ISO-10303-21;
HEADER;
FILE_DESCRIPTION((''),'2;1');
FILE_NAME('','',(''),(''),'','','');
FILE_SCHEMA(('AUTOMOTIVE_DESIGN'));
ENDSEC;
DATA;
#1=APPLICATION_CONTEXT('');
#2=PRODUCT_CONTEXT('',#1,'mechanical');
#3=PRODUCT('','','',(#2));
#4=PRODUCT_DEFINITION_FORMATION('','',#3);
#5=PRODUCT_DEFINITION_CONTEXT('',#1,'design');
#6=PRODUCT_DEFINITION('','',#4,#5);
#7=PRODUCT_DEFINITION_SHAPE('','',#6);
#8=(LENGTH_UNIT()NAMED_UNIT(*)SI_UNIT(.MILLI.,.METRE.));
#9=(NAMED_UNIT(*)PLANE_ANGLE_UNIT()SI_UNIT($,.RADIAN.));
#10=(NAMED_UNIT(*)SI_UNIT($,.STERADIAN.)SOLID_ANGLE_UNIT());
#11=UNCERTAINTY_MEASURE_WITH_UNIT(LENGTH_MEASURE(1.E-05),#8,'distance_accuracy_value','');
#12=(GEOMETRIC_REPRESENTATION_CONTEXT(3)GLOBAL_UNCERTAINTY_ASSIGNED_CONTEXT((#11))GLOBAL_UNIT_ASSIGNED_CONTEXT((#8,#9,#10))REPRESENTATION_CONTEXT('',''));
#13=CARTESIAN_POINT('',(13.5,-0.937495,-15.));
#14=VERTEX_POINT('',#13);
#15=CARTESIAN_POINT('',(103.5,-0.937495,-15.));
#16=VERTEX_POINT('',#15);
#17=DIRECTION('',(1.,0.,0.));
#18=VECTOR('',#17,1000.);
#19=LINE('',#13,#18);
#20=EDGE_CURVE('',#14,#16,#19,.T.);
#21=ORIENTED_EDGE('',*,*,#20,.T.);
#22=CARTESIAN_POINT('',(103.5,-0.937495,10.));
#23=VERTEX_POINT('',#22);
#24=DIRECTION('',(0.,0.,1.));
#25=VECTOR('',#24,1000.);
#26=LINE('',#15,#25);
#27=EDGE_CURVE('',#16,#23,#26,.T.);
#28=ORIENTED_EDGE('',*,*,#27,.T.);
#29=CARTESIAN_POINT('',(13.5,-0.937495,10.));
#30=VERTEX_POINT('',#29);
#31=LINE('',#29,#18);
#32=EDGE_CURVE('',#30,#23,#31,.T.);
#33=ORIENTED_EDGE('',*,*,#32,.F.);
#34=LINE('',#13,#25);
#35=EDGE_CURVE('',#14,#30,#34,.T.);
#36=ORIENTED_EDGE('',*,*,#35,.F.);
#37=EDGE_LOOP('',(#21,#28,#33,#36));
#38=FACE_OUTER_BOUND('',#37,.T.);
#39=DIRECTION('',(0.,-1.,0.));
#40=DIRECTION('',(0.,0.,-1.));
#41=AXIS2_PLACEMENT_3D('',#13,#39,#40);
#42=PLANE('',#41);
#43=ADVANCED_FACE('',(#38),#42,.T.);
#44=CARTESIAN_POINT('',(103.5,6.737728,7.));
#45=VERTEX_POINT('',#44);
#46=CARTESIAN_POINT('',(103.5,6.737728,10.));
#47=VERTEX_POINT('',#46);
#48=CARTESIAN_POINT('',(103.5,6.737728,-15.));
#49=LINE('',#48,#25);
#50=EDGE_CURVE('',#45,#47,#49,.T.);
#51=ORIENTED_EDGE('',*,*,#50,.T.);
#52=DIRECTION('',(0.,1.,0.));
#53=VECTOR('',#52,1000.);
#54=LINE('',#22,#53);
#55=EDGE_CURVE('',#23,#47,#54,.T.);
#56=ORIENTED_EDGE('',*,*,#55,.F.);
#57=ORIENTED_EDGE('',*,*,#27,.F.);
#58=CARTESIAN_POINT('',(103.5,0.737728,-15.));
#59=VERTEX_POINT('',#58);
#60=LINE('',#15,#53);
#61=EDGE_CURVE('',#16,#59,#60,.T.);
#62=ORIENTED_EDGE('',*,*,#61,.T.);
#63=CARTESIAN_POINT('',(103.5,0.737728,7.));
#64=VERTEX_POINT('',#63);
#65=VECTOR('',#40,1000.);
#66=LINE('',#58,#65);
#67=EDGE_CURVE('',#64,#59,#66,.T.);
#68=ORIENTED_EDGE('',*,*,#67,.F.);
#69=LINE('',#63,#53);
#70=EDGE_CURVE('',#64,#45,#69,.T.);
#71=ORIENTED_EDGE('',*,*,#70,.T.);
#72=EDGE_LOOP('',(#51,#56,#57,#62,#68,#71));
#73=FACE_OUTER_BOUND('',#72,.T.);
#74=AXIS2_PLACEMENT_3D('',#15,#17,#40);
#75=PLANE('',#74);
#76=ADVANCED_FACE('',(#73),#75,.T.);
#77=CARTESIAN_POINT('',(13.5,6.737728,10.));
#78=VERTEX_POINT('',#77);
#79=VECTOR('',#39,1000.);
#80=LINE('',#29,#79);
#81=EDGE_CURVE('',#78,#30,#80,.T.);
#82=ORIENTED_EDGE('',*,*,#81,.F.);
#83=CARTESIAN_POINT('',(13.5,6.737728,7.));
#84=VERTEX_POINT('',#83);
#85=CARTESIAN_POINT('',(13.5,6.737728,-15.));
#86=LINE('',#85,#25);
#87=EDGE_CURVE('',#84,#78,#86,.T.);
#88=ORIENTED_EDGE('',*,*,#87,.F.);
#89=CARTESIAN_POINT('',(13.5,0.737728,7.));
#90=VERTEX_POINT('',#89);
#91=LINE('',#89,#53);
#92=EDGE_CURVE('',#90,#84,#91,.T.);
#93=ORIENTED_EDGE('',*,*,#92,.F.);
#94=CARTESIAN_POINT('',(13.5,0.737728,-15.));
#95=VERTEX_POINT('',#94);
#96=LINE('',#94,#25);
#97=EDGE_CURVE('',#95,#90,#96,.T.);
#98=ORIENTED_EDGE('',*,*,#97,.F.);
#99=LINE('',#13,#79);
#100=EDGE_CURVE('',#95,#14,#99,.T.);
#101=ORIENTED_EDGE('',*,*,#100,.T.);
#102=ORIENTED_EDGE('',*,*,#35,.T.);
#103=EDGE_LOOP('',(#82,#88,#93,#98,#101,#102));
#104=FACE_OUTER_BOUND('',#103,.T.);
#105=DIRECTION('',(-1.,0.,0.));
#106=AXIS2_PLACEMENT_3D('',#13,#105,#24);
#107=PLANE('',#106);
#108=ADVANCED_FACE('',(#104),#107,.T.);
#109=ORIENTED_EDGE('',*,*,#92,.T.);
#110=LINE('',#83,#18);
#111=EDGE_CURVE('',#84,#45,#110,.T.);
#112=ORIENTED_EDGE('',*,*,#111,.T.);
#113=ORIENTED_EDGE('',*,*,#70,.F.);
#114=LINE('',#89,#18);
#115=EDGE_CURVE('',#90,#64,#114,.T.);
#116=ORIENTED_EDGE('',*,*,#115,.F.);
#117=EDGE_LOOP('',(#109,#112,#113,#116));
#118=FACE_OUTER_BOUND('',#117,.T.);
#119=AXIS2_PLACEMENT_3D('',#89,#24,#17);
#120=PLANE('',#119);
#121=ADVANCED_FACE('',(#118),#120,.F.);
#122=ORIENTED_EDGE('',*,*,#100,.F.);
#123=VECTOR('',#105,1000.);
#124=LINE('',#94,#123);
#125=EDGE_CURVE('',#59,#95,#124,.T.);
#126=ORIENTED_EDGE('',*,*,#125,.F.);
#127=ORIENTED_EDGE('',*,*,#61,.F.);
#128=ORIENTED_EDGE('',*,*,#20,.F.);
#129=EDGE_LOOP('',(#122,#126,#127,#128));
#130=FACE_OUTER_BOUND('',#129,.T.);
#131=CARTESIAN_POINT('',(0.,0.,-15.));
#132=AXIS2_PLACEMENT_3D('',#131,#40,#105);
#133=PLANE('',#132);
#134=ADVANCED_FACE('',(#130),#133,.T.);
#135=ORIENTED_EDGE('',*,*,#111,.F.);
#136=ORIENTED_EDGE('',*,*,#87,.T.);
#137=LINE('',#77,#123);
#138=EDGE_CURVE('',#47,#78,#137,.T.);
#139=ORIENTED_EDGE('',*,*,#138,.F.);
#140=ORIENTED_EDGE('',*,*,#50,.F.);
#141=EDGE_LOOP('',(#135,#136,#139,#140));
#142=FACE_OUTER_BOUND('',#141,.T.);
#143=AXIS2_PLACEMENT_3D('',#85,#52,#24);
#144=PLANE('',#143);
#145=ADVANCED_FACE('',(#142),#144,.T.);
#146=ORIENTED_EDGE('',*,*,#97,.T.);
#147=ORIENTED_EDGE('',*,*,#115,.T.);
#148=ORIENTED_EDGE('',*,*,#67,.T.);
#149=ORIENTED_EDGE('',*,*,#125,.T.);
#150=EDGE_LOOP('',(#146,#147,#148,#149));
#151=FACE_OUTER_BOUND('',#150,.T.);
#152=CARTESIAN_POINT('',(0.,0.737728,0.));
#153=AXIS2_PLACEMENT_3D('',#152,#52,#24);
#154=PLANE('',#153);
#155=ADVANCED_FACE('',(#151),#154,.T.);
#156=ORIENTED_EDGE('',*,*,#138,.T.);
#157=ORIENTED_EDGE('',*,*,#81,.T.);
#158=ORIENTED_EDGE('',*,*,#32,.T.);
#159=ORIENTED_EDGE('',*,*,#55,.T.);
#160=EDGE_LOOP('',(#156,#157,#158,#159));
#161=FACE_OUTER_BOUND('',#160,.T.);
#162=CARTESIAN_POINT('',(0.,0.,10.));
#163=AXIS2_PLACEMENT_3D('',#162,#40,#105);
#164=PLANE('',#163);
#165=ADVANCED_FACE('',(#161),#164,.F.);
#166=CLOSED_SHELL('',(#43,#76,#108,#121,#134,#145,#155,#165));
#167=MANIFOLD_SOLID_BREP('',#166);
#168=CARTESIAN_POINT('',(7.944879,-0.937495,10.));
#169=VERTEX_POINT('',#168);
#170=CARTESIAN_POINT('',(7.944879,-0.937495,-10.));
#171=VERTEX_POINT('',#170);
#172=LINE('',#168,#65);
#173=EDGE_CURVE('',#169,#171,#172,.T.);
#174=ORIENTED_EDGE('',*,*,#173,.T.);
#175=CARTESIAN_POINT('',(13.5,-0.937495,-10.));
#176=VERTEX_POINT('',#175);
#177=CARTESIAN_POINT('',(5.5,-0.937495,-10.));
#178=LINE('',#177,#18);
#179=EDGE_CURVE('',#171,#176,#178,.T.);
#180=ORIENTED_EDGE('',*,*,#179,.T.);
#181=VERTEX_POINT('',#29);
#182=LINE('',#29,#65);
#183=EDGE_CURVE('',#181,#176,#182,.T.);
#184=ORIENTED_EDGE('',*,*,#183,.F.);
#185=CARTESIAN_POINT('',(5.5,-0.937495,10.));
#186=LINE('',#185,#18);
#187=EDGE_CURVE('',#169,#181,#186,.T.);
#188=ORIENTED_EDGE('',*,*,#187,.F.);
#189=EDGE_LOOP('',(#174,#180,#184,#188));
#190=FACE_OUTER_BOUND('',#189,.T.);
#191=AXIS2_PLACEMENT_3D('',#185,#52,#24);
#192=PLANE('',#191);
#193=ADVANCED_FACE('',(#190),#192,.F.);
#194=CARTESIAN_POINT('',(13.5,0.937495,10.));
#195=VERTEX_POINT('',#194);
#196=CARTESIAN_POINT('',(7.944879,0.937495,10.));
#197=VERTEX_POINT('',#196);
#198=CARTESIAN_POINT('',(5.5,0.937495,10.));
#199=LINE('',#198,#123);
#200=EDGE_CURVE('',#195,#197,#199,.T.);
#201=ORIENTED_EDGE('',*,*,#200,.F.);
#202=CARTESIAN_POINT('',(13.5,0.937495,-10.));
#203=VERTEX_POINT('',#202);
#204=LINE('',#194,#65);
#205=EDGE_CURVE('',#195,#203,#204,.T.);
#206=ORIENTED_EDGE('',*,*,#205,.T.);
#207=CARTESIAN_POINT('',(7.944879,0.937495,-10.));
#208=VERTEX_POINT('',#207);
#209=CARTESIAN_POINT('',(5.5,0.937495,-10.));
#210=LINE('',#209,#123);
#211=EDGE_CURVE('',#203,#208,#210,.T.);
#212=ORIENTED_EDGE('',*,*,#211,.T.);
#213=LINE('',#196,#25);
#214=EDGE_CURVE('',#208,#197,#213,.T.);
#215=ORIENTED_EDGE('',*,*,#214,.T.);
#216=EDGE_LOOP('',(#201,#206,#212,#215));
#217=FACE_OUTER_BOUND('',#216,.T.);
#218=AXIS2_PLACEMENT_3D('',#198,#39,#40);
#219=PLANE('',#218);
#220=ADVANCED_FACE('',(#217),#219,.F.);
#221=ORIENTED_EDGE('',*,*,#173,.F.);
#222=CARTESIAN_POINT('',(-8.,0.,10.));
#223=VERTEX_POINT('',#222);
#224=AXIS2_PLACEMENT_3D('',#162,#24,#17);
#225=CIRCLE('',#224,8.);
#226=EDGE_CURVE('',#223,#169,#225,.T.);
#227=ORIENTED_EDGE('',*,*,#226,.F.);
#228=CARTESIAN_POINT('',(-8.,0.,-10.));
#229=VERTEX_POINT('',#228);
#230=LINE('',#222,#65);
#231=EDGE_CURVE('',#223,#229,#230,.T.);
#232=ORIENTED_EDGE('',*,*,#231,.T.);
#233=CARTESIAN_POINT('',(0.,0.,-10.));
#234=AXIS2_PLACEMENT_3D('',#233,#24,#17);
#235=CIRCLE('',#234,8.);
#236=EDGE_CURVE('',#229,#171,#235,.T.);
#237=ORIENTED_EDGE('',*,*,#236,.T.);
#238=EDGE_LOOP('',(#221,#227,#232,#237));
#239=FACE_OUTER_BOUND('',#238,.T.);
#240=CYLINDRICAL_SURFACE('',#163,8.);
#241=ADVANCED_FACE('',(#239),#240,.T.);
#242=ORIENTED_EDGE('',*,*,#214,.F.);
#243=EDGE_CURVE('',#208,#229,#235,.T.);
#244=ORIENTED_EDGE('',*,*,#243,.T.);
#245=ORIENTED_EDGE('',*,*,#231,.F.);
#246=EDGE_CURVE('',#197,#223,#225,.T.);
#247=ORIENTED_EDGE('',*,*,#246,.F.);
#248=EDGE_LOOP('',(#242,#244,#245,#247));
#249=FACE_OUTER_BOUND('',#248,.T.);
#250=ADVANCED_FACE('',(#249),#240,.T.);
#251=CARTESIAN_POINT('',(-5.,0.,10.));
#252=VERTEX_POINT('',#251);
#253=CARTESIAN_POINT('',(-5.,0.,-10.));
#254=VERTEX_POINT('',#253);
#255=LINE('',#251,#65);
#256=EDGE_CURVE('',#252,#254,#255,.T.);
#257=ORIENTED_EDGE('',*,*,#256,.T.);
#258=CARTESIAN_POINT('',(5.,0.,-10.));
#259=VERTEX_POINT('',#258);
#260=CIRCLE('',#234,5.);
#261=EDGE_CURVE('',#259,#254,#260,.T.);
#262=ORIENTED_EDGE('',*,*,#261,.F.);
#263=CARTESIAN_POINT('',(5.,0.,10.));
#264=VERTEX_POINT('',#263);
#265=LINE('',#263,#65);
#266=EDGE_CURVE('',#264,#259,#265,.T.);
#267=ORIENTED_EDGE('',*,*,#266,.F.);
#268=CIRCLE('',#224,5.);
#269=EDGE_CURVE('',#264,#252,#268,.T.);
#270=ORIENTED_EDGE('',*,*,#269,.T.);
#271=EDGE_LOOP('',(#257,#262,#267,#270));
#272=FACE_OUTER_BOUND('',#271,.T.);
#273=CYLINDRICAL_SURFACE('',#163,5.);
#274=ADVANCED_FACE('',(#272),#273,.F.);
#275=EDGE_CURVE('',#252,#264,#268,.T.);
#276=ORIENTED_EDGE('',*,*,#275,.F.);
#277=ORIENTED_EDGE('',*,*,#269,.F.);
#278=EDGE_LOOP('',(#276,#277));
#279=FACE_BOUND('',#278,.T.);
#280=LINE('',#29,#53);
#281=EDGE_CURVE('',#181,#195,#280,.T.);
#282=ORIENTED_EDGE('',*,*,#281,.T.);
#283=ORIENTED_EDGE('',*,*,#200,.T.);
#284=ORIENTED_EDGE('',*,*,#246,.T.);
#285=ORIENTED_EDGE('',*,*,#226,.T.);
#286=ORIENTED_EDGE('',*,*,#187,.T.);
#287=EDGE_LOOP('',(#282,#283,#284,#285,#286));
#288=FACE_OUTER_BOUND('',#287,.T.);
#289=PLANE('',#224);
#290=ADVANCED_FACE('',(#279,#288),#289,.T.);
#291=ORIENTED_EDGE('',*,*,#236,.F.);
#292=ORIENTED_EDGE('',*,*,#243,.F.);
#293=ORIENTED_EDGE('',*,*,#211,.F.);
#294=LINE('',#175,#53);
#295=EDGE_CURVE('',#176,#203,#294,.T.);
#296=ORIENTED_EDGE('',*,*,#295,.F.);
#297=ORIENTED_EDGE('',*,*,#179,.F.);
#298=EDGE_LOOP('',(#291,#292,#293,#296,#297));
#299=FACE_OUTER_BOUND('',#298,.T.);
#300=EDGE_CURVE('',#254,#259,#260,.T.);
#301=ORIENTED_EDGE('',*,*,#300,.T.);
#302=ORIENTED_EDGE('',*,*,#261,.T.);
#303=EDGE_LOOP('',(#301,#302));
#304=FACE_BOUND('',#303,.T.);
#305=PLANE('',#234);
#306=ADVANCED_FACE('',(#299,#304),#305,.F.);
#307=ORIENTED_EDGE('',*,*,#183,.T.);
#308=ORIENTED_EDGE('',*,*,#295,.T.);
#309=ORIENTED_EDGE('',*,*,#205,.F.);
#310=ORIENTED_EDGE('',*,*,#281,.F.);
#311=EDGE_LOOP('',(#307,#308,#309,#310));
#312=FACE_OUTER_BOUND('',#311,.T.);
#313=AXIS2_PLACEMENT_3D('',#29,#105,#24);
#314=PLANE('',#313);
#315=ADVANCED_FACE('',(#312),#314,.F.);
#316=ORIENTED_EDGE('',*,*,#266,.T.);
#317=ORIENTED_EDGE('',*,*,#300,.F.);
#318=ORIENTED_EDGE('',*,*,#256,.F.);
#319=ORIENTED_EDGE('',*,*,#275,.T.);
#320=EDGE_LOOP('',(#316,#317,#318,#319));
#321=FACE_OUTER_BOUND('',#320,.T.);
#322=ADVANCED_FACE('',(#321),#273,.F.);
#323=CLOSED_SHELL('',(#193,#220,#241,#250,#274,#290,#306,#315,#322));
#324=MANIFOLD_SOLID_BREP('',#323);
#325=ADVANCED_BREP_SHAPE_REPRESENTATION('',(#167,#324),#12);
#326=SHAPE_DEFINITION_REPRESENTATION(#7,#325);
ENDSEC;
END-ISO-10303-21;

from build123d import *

# Parameters (mm, degrees)
SKETCH1_R           = 8
SKETCH1_R_2         = 5
BOSS_EXTRUDE1_DEPTH = 10
SKETCH3_W           = 8
SKETCH3_H           = 1.874989596
BOSS_EXTRUDE2_DEPTH = 10
SKETCH4_W           = 90
SKETCH4_H           = 7.675222422
BOSS_EXTRUDE3_DEPTH = 25
SKETCH5_W           = 90
SKETCH5_H           = 22
CUT_EXTRUDE1_DEPTH  = 6


with BuildPart() as part:
    # Sketch1 → Boss-Extrude1 (new, symmetric)
    with BuildSketch(Plane.XY):
        Circle(SKETCH1_R)
        Circle(SKETCH1_R_2, mode=Mode.SUBTRACT)
    extrude(amount=BOSS_EXTRUDE1_DEPTH, both=True)

    # Sketch3 → Boss-Extrude2 (add, symmetric)
    with BuildSketch(Plane.XY):
        with Locations((9.5, 0)):
            Rectangle(SKETCH3_W, SKETCH3_H)
    extrude(amount=BOSS_EXTRUDE2_DEPTH, both=True)


with BuildPart() as body_2:
    # Sketch4 → Boss-Extrude3 (new body)
    with BuildSketch(Plane.XY.offset(10)):
        with Locations((58.5, 2.900116413)):
            Rectangle(SKETCH4_W, SKETCH4_H)
    extrude(amount=-BOSS_EXTRUDE3_DEPTH)

    # Sketch5 → Cut-Extrude1 (cut)
    with BuildSketch(Plane(origin=(0, 6.737727624, 0), x_dir=(1, 0, 0), z_dir=(0, 1, 0))):
        with Locations((58.5, 4)):
            Rectangle(SKETCH5_W, SKETCH5_H)
    extrude(amount=-CUT_EXTRUDE1_DEPTH, mode=Mode.SUBTRACT)


solid = Compound([part.part, body_2.part])
